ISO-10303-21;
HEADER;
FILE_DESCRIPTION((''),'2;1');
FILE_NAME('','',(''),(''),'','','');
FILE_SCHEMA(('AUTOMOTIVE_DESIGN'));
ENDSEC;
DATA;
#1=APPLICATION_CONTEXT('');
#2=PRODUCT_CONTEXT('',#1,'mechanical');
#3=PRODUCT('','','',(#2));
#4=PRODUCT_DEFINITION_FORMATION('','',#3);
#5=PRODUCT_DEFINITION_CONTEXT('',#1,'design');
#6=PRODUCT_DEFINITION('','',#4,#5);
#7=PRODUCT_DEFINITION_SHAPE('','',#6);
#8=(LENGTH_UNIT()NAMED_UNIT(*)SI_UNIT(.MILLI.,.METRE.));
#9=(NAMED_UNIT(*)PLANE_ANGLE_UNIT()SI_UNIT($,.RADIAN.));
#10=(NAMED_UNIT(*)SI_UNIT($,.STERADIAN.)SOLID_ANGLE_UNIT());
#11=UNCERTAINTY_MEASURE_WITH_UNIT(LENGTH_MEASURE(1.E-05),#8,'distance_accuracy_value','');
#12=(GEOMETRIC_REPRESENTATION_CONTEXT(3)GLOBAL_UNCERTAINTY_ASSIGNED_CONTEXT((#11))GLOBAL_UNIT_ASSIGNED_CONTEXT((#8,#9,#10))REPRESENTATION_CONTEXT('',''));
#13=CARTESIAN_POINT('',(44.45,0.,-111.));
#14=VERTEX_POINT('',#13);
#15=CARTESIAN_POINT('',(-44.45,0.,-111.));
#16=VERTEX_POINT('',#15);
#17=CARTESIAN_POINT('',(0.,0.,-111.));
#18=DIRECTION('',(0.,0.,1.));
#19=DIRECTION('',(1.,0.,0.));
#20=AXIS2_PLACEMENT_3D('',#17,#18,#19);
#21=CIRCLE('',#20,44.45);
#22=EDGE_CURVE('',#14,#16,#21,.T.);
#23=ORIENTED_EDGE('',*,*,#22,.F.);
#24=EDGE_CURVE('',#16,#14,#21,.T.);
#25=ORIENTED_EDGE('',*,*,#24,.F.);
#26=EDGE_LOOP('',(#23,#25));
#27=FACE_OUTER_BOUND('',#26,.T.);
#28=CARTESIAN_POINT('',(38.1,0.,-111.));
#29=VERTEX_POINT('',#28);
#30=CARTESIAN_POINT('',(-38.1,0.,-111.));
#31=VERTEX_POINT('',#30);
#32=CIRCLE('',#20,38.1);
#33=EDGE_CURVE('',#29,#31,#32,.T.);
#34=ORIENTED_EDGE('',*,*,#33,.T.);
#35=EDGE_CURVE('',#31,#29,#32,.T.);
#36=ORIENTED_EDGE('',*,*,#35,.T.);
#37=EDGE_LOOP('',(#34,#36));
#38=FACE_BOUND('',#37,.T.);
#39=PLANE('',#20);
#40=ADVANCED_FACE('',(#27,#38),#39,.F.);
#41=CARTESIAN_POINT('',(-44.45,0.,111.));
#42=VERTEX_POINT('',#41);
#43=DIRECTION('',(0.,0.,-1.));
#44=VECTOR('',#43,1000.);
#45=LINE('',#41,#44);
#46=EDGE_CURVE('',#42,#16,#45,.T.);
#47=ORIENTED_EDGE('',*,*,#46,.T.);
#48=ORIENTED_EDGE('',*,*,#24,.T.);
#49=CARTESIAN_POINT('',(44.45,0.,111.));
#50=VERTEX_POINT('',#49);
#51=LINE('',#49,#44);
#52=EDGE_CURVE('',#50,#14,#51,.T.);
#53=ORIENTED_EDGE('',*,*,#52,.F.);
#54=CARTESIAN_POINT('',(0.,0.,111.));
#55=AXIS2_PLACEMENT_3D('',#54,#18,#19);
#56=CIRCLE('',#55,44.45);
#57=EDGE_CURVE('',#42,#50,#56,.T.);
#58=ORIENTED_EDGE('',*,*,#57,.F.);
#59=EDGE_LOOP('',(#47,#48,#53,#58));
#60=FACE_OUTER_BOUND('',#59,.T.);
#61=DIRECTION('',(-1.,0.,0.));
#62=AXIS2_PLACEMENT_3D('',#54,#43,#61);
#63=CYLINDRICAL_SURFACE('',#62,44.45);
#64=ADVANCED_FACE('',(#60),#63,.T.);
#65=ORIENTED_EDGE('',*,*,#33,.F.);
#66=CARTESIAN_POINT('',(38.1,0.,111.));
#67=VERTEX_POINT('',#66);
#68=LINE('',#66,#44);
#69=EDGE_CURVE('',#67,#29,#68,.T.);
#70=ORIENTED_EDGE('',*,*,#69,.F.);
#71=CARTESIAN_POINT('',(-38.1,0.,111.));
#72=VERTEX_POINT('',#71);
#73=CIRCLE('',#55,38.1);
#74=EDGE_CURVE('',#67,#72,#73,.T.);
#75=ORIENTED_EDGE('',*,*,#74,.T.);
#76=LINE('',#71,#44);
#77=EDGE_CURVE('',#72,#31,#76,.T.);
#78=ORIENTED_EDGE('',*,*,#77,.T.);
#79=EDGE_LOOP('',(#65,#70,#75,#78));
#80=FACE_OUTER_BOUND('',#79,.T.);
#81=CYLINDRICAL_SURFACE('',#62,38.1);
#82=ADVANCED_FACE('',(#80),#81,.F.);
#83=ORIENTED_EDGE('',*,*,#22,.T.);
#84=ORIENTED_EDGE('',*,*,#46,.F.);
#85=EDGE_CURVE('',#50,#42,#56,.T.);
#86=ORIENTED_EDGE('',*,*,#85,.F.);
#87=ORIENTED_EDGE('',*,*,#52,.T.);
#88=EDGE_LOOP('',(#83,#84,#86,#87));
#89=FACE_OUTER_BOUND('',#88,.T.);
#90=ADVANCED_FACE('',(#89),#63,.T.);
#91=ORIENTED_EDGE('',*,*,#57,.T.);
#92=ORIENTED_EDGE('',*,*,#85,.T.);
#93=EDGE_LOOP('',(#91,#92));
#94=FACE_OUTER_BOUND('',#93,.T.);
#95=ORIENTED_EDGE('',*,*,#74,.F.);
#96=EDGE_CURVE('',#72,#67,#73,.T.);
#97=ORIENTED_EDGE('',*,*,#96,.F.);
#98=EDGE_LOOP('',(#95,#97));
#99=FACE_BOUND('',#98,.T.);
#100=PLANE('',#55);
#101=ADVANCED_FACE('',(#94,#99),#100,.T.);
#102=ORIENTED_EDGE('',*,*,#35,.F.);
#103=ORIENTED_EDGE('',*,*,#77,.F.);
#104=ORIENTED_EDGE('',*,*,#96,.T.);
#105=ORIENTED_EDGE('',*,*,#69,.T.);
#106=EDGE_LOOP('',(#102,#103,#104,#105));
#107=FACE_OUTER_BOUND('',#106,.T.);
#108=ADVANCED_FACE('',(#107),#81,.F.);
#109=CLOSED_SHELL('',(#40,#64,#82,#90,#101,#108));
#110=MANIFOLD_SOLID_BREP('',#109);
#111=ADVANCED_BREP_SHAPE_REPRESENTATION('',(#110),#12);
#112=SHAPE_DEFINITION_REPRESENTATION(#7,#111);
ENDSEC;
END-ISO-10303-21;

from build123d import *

# Parameters (mm, degrees)
SKETCH_1_R      = 44.45
SKETCH_1_R_2    = 38.1
EXTRUDE_1_DEPTH = 111


with BuildPart() as part:
    # 草图1 → 凸台-拉伸1 (new, symmetric)
    with BuildSketch(Plane.XY):
        Circle(SKETCH_1_R)
        Circle(SKETCH_1_R_2, mode=Mode.SUBTRACT)
    extrude(amount=EXTRUDE_1_DEPTH, both=True)


solid = part.part
